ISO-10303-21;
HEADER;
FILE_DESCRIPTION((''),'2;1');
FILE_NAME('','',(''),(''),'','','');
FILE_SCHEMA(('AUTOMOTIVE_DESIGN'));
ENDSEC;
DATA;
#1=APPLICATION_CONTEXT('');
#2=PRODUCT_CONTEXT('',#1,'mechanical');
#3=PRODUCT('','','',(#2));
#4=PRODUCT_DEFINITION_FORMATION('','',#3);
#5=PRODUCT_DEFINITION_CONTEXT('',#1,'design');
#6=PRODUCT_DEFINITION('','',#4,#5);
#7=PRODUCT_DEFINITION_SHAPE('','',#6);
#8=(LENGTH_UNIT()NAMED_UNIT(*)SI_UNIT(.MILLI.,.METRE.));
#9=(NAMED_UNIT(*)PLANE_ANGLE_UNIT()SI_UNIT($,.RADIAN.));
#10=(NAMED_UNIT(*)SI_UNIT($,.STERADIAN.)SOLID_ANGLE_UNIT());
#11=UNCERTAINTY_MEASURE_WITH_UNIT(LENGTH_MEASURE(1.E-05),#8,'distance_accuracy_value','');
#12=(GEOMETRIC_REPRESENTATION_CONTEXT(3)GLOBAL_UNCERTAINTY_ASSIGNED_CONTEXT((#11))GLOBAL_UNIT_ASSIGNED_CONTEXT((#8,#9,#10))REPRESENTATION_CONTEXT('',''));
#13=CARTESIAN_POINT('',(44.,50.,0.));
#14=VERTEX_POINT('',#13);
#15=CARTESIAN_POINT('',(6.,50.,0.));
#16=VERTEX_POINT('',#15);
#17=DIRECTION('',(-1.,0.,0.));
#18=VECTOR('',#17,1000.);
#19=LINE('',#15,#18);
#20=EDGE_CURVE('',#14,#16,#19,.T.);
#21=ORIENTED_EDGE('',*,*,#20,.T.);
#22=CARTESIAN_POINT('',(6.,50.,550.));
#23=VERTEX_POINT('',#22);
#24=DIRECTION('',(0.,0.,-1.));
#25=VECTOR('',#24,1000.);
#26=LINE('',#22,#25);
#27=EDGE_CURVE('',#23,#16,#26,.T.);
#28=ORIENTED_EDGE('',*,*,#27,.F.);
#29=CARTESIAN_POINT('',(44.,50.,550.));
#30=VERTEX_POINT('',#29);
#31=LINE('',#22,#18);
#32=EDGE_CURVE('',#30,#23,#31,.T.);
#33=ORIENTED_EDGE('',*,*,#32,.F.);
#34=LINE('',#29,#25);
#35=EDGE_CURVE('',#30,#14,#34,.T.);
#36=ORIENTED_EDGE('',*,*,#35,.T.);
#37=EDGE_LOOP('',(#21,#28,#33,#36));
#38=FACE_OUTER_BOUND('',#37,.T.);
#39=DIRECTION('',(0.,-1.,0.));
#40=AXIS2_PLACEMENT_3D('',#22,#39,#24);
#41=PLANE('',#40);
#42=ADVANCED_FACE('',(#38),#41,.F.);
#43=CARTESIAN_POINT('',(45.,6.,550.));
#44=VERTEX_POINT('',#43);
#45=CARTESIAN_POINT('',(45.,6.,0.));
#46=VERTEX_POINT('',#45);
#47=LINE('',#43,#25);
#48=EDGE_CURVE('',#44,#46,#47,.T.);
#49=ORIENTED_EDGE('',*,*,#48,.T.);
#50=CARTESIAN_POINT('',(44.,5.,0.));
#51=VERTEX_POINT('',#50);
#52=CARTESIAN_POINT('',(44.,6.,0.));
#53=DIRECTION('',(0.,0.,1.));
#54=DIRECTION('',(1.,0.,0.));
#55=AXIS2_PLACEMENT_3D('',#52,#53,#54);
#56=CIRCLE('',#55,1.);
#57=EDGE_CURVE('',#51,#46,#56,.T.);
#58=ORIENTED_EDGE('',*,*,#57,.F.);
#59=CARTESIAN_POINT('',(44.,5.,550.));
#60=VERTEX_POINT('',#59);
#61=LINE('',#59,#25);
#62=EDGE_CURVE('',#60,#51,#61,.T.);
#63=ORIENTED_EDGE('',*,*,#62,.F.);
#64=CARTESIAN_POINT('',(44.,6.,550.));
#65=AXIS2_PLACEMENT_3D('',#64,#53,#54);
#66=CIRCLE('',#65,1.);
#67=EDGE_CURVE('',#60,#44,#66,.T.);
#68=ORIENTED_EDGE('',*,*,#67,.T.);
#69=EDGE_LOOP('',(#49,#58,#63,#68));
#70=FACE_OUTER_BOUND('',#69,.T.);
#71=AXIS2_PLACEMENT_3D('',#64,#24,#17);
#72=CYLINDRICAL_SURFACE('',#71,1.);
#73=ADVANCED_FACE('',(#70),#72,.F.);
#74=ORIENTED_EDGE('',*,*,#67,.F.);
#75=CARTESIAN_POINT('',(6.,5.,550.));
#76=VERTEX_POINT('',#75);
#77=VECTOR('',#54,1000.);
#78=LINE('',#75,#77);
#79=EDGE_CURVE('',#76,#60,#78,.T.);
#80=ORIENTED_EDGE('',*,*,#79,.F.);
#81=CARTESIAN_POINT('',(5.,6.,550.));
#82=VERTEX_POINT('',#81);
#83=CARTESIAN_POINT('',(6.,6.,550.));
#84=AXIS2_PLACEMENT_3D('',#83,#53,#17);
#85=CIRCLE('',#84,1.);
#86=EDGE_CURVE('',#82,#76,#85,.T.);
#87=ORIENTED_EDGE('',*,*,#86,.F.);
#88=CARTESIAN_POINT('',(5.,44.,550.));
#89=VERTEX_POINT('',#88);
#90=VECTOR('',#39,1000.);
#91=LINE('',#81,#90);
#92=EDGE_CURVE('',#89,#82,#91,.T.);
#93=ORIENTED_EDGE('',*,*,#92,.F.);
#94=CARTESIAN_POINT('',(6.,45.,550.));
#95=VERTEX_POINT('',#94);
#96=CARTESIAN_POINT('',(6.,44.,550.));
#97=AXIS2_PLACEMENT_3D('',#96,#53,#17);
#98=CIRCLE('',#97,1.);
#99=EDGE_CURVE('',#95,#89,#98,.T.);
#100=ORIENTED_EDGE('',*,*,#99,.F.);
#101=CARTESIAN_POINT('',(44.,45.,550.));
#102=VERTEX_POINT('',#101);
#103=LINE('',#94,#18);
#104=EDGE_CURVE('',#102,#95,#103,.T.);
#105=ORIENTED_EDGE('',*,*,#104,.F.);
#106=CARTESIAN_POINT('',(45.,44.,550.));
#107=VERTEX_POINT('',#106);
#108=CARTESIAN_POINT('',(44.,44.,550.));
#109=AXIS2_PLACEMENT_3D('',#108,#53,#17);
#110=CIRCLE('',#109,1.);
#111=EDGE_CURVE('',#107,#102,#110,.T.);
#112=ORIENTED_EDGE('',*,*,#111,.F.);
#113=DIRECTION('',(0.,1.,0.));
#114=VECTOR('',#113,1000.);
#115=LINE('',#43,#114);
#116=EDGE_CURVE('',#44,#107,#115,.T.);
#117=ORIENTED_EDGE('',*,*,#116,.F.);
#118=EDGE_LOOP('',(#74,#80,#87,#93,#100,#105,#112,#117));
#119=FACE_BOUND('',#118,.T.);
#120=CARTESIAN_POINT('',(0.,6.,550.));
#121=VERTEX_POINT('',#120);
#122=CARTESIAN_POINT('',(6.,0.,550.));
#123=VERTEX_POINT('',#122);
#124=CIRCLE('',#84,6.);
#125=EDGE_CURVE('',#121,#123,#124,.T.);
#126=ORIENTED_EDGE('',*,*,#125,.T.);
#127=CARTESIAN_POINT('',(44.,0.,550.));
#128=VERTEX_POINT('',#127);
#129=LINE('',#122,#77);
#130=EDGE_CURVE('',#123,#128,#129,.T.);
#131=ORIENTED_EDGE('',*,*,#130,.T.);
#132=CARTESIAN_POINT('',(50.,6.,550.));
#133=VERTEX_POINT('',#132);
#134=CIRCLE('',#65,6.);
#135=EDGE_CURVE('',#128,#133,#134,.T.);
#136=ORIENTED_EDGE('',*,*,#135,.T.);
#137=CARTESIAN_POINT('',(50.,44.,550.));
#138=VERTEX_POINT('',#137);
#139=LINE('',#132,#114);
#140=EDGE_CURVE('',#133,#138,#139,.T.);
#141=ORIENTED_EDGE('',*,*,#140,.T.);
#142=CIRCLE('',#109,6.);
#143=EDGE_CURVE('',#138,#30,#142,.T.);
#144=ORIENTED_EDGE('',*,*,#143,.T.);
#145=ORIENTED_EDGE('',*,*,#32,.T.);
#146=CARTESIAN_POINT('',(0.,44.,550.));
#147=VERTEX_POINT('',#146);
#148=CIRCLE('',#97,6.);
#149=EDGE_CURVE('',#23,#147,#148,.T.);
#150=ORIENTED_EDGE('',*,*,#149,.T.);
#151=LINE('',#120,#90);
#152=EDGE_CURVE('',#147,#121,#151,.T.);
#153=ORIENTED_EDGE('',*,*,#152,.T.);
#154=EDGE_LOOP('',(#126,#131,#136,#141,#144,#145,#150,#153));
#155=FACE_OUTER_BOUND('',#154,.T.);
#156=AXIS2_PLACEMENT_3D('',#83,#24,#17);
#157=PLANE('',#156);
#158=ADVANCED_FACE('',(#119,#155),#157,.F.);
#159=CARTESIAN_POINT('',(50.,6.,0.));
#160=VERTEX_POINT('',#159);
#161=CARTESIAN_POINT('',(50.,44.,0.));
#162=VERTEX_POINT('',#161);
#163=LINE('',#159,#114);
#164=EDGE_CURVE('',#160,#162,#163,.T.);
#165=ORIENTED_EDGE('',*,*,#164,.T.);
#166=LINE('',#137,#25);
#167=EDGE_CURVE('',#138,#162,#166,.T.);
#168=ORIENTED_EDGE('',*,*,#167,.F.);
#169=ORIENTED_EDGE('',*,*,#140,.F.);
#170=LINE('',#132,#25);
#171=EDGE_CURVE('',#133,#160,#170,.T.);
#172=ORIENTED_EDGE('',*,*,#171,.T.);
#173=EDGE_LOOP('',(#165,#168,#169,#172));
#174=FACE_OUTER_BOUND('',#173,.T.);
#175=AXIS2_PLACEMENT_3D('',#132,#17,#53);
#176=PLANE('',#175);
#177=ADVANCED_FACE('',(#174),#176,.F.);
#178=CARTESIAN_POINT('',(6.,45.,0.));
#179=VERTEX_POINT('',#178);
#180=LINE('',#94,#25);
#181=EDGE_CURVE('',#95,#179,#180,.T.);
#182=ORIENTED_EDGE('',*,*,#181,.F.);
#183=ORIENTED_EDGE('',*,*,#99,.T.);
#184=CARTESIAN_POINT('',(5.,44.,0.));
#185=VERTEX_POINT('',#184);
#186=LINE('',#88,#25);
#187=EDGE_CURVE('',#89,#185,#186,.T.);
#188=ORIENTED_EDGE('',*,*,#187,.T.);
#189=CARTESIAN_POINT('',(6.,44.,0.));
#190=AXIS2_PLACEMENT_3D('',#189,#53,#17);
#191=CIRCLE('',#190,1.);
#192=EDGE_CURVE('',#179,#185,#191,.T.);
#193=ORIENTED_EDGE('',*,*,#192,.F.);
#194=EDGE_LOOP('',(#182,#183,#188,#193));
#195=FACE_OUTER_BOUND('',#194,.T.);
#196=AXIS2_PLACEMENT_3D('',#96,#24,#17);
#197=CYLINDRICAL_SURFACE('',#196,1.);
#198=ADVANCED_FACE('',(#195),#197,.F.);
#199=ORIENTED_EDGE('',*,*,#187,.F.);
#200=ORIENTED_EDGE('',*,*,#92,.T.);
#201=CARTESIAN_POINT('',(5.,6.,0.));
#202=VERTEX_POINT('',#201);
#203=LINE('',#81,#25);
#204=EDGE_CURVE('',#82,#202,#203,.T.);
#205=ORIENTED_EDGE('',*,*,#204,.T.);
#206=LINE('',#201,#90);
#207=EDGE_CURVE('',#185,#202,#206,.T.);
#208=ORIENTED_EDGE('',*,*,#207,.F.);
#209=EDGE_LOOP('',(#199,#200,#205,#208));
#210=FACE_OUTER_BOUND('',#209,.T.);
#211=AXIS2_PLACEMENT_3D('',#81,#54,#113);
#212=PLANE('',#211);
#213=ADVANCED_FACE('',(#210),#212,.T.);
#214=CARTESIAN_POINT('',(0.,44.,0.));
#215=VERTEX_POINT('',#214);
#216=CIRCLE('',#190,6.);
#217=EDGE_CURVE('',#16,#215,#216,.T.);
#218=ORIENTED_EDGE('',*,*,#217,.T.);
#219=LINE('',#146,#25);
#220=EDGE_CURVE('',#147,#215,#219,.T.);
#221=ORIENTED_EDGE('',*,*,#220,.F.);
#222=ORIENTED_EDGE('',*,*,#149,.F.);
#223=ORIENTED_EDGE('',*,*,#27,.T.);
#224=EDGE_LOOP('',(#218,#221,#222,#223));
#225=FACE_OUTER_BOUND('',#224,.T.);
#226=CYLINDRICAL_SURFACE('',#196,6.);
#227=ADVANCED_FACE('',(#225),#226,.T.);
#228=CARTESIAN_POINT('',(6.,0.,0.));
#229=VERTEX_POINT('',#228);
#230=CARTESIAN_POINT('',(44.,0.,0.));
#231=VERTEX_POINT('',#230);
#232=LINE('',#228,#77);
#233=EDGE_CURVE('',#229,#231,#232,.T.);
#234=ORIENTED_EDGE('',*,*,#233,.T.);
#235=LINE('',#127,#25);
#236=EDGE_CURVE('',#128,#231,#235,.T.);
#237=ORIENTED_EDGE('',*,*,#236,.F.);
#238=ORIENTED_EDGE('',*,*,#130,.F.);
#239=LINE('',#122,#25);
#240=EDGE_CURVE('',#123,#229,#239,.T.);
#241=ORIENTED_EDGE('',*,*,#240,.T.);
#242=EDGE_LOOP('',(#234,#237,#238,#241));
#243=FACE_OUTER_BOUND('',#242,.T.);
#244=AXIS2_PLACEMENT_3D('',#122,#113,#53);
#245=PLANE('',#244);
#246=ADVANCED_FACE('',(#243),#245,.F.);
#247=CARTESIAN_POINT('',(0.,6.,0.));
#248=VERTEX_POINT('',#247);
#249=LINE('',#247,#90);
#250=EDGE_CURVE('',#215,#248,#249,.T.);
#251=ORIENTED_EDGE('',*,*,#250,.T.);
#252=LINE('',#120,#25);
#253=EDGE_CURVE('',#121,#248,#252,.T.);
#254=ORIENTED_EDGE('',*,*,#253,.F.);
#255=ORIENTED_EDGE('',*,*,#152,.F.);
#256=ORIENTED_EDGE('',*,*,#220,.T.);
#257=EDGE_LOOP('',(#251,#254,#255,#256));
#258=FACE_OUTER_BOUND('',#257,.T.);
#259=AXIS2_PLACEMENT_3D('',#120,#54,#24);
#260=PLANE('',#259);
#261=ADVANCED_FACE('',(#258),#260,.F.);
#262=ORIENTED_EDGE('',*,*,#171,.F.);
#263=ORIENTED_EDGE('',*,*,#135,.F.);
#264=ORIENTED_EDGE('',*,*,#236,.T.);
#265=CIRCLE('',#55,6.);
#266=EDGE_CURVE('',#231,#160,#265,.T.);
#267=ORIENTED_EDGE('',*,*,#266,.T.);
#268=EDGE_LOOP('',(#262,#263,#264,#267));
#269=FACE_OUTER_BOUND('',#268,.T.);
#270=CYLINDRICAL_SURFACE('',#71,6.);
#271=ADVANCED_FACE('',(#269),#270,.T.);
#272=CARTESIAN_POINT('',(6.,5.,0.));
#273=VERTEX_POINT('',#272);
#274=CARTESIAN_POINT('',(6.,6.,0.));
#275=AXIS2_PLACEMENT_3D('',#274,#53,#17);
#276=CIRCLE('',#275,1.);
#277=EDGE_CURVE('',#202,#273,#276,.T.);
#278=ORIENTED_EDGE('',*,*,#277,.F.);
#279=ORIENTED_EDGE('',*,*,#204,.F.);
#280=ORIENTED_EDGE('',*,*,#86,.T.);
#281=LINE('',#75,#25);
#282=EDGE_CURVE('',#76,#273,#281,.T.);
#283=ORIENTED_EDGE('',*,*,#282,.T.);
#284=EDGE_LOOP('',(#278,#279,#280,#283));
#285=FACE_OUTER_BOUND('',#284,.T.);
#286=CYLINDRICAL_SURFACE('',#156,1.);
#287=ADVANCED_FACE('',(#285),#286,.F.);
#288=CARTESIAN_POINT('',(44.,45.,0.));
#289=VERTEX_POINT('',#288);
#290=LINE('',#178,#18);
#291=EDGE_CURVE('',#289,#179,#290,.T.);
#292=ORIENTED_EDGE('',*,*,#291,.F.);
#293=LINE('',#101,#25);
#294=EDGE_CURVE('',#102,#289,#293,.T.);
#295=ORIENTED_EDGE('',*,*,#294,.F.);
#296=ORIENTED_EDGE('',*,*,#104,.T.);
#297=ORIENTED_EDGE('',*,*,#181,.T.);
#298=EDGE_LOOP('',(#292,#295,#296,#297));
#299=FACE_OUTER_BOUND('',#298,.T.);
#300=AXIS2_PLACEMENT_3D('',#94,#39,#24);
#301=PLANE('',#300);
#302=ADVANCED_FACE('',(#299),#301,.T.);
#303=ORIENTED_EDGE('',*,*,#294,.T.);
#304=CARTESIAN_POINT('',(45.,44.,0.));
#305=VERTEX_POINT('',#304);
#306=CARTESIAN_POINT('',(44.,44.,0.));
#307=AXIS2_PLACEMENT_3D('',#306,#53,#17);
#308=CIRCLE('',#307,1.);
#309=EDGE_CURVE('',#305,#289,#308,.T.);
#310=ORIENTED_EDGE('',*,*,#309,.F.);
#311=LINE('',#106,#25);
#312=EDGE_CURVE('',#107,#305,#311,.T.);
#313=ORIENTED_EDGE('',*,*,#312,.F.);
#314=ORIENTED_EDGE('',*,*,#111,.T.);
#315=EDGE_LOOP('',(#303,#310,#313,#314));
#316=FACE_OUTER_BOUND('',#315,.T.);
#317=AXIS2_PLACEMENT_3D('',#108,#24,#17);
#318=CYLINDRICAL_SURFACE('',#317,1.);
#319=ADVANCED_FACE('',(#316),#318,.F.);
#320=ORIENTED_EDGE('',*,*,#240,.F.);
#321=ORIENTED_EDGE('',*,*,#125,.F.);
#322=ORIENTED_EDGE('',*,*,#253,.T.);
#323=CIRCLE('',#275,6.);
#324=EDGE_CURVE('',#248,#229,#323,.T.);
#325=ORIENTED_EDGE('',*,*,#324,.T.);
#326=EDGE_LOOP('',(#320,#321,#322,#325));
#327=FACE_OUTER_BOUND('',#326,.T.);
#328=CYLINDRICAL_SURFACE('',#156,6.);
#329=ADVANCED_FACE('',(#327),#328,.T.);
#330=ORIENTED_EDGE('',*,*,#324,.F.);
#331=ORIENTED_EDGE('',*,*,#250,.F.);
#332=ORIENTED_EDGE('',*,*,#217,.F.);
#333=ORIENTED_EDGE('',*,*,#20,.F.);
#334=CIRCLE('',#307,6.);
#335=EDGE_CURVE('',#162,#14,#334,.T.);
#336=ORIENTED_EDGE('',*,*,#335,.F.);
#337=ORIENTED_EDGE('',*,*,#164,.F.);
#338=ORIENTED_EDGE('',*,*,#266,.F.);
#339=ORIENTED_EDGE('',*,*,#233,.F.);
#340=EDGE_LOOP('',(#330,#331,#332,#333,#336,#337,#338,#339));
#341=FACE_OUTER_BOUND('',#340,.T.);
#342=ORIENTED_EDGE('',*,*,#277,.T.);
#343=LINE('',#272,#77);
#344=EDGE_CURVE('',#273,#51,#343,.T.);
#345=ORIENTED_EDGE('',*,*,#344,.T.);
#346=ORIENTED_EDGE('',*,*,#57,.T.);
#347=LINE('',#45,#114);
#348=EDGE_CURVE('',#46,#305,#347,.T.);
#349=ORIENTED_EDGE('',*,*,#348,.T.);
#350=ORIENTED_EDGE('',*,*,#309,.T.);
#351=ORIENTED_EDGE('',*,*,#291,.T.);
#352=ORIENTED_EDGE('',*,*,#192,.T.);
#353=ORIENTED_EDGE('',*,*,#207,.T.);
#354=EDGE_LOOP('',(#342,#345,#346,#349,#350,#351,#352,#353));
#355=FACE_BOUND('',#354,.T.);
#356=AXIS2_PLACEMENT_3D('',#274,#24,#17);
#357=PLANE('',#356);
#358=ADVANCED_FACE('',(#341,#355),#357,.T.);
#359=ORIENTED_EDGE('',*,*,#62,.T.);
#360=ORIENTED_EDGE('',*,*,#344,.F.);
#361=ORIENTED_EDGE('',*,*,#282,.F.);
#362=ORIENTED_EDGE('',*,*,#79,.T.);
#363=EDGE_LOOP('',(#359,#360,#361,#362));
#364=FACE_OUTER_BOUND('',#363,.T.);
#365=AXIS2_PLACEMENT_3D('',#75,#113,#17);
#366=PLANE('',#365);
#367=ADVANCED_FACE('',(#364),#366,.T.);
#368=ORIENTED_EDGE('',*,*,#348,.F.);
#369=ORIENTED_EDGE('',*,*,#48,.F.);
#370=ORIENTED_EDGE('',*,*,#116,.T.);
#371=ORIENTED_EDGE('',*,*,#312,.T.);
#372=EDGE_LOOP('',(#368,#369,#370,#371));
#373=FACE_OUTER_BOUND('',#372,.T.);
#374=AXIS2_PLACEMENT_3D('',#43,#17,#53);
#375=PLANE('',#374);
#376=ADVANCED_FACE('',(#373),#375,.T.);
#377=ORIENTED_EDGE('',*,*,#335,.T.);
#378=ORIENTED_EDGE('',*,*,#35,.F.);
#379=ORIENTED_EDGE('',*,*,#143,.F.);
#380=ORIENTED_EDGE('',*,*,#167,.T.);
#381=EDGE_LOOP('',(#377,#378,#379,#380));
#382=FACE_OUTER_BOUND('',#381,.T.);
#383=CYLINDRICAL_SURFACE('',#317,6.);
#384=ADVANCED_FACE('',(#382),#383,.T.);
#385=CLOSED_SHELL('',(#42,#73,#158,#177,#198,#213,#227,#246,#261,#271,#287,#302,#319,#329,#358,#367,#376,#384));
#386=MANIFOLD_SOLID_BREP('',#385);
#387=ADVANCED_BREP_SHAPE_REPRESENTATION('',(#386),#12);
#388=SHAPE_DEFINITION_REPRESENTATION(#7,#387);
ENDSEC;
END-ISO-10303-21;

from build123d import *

# Parameters (mm, degrees)
BOSS_EXTRUDE1_DEPTH = 550


with BuildPart() as part:
    # Sketch1 → Boss-Extrude1 (new body)
    with BuildSketch(Plane.XY):
        with BuildLine():
            Line((6, 0), (44, 0))
            ThreePointArc((44, 0), (48.242640687, 1.757359313), (50, 6))
            Line((50, 6), (50, 44))
            ThreePointArc((50, 44), (48.242640687, 48.242640687), (44, 50))
            Line((44, 50), (6, 50))
            ThreePointArc((6, 50), (1.757359313, 48.242640687), (0, 44))
            Line((0, 44), (0, 6))
            ThreePointArc((0, 6), (1.757359313, 1.757359313), (6, 0))
        make_face()
        with BuildLine():
            Line((6, 45), (44, 45))
            ThreePointArc((44, 45), (44.707106781, 44.707106781), (45, 44))
            Line((45, 44), (45, 6))
            ThreePointArc((45, 6), (44.707106781, 5.292893219), (44, 5))
            Line((44, 5), (6, 5))
            ThreePointArc((6, 5), (5.292893219, 5.292893219), (5, 6))
            Line((5, 6), (5, 44))
            ThreePointArc((5, 44), (5.292893219, 44.707106781), (6, 45))
        make_face(mode=Mode.SUBTRACT)
    extrude(amount=BOSS_EXTRUDE1_DEPTH)


solid = part.part
